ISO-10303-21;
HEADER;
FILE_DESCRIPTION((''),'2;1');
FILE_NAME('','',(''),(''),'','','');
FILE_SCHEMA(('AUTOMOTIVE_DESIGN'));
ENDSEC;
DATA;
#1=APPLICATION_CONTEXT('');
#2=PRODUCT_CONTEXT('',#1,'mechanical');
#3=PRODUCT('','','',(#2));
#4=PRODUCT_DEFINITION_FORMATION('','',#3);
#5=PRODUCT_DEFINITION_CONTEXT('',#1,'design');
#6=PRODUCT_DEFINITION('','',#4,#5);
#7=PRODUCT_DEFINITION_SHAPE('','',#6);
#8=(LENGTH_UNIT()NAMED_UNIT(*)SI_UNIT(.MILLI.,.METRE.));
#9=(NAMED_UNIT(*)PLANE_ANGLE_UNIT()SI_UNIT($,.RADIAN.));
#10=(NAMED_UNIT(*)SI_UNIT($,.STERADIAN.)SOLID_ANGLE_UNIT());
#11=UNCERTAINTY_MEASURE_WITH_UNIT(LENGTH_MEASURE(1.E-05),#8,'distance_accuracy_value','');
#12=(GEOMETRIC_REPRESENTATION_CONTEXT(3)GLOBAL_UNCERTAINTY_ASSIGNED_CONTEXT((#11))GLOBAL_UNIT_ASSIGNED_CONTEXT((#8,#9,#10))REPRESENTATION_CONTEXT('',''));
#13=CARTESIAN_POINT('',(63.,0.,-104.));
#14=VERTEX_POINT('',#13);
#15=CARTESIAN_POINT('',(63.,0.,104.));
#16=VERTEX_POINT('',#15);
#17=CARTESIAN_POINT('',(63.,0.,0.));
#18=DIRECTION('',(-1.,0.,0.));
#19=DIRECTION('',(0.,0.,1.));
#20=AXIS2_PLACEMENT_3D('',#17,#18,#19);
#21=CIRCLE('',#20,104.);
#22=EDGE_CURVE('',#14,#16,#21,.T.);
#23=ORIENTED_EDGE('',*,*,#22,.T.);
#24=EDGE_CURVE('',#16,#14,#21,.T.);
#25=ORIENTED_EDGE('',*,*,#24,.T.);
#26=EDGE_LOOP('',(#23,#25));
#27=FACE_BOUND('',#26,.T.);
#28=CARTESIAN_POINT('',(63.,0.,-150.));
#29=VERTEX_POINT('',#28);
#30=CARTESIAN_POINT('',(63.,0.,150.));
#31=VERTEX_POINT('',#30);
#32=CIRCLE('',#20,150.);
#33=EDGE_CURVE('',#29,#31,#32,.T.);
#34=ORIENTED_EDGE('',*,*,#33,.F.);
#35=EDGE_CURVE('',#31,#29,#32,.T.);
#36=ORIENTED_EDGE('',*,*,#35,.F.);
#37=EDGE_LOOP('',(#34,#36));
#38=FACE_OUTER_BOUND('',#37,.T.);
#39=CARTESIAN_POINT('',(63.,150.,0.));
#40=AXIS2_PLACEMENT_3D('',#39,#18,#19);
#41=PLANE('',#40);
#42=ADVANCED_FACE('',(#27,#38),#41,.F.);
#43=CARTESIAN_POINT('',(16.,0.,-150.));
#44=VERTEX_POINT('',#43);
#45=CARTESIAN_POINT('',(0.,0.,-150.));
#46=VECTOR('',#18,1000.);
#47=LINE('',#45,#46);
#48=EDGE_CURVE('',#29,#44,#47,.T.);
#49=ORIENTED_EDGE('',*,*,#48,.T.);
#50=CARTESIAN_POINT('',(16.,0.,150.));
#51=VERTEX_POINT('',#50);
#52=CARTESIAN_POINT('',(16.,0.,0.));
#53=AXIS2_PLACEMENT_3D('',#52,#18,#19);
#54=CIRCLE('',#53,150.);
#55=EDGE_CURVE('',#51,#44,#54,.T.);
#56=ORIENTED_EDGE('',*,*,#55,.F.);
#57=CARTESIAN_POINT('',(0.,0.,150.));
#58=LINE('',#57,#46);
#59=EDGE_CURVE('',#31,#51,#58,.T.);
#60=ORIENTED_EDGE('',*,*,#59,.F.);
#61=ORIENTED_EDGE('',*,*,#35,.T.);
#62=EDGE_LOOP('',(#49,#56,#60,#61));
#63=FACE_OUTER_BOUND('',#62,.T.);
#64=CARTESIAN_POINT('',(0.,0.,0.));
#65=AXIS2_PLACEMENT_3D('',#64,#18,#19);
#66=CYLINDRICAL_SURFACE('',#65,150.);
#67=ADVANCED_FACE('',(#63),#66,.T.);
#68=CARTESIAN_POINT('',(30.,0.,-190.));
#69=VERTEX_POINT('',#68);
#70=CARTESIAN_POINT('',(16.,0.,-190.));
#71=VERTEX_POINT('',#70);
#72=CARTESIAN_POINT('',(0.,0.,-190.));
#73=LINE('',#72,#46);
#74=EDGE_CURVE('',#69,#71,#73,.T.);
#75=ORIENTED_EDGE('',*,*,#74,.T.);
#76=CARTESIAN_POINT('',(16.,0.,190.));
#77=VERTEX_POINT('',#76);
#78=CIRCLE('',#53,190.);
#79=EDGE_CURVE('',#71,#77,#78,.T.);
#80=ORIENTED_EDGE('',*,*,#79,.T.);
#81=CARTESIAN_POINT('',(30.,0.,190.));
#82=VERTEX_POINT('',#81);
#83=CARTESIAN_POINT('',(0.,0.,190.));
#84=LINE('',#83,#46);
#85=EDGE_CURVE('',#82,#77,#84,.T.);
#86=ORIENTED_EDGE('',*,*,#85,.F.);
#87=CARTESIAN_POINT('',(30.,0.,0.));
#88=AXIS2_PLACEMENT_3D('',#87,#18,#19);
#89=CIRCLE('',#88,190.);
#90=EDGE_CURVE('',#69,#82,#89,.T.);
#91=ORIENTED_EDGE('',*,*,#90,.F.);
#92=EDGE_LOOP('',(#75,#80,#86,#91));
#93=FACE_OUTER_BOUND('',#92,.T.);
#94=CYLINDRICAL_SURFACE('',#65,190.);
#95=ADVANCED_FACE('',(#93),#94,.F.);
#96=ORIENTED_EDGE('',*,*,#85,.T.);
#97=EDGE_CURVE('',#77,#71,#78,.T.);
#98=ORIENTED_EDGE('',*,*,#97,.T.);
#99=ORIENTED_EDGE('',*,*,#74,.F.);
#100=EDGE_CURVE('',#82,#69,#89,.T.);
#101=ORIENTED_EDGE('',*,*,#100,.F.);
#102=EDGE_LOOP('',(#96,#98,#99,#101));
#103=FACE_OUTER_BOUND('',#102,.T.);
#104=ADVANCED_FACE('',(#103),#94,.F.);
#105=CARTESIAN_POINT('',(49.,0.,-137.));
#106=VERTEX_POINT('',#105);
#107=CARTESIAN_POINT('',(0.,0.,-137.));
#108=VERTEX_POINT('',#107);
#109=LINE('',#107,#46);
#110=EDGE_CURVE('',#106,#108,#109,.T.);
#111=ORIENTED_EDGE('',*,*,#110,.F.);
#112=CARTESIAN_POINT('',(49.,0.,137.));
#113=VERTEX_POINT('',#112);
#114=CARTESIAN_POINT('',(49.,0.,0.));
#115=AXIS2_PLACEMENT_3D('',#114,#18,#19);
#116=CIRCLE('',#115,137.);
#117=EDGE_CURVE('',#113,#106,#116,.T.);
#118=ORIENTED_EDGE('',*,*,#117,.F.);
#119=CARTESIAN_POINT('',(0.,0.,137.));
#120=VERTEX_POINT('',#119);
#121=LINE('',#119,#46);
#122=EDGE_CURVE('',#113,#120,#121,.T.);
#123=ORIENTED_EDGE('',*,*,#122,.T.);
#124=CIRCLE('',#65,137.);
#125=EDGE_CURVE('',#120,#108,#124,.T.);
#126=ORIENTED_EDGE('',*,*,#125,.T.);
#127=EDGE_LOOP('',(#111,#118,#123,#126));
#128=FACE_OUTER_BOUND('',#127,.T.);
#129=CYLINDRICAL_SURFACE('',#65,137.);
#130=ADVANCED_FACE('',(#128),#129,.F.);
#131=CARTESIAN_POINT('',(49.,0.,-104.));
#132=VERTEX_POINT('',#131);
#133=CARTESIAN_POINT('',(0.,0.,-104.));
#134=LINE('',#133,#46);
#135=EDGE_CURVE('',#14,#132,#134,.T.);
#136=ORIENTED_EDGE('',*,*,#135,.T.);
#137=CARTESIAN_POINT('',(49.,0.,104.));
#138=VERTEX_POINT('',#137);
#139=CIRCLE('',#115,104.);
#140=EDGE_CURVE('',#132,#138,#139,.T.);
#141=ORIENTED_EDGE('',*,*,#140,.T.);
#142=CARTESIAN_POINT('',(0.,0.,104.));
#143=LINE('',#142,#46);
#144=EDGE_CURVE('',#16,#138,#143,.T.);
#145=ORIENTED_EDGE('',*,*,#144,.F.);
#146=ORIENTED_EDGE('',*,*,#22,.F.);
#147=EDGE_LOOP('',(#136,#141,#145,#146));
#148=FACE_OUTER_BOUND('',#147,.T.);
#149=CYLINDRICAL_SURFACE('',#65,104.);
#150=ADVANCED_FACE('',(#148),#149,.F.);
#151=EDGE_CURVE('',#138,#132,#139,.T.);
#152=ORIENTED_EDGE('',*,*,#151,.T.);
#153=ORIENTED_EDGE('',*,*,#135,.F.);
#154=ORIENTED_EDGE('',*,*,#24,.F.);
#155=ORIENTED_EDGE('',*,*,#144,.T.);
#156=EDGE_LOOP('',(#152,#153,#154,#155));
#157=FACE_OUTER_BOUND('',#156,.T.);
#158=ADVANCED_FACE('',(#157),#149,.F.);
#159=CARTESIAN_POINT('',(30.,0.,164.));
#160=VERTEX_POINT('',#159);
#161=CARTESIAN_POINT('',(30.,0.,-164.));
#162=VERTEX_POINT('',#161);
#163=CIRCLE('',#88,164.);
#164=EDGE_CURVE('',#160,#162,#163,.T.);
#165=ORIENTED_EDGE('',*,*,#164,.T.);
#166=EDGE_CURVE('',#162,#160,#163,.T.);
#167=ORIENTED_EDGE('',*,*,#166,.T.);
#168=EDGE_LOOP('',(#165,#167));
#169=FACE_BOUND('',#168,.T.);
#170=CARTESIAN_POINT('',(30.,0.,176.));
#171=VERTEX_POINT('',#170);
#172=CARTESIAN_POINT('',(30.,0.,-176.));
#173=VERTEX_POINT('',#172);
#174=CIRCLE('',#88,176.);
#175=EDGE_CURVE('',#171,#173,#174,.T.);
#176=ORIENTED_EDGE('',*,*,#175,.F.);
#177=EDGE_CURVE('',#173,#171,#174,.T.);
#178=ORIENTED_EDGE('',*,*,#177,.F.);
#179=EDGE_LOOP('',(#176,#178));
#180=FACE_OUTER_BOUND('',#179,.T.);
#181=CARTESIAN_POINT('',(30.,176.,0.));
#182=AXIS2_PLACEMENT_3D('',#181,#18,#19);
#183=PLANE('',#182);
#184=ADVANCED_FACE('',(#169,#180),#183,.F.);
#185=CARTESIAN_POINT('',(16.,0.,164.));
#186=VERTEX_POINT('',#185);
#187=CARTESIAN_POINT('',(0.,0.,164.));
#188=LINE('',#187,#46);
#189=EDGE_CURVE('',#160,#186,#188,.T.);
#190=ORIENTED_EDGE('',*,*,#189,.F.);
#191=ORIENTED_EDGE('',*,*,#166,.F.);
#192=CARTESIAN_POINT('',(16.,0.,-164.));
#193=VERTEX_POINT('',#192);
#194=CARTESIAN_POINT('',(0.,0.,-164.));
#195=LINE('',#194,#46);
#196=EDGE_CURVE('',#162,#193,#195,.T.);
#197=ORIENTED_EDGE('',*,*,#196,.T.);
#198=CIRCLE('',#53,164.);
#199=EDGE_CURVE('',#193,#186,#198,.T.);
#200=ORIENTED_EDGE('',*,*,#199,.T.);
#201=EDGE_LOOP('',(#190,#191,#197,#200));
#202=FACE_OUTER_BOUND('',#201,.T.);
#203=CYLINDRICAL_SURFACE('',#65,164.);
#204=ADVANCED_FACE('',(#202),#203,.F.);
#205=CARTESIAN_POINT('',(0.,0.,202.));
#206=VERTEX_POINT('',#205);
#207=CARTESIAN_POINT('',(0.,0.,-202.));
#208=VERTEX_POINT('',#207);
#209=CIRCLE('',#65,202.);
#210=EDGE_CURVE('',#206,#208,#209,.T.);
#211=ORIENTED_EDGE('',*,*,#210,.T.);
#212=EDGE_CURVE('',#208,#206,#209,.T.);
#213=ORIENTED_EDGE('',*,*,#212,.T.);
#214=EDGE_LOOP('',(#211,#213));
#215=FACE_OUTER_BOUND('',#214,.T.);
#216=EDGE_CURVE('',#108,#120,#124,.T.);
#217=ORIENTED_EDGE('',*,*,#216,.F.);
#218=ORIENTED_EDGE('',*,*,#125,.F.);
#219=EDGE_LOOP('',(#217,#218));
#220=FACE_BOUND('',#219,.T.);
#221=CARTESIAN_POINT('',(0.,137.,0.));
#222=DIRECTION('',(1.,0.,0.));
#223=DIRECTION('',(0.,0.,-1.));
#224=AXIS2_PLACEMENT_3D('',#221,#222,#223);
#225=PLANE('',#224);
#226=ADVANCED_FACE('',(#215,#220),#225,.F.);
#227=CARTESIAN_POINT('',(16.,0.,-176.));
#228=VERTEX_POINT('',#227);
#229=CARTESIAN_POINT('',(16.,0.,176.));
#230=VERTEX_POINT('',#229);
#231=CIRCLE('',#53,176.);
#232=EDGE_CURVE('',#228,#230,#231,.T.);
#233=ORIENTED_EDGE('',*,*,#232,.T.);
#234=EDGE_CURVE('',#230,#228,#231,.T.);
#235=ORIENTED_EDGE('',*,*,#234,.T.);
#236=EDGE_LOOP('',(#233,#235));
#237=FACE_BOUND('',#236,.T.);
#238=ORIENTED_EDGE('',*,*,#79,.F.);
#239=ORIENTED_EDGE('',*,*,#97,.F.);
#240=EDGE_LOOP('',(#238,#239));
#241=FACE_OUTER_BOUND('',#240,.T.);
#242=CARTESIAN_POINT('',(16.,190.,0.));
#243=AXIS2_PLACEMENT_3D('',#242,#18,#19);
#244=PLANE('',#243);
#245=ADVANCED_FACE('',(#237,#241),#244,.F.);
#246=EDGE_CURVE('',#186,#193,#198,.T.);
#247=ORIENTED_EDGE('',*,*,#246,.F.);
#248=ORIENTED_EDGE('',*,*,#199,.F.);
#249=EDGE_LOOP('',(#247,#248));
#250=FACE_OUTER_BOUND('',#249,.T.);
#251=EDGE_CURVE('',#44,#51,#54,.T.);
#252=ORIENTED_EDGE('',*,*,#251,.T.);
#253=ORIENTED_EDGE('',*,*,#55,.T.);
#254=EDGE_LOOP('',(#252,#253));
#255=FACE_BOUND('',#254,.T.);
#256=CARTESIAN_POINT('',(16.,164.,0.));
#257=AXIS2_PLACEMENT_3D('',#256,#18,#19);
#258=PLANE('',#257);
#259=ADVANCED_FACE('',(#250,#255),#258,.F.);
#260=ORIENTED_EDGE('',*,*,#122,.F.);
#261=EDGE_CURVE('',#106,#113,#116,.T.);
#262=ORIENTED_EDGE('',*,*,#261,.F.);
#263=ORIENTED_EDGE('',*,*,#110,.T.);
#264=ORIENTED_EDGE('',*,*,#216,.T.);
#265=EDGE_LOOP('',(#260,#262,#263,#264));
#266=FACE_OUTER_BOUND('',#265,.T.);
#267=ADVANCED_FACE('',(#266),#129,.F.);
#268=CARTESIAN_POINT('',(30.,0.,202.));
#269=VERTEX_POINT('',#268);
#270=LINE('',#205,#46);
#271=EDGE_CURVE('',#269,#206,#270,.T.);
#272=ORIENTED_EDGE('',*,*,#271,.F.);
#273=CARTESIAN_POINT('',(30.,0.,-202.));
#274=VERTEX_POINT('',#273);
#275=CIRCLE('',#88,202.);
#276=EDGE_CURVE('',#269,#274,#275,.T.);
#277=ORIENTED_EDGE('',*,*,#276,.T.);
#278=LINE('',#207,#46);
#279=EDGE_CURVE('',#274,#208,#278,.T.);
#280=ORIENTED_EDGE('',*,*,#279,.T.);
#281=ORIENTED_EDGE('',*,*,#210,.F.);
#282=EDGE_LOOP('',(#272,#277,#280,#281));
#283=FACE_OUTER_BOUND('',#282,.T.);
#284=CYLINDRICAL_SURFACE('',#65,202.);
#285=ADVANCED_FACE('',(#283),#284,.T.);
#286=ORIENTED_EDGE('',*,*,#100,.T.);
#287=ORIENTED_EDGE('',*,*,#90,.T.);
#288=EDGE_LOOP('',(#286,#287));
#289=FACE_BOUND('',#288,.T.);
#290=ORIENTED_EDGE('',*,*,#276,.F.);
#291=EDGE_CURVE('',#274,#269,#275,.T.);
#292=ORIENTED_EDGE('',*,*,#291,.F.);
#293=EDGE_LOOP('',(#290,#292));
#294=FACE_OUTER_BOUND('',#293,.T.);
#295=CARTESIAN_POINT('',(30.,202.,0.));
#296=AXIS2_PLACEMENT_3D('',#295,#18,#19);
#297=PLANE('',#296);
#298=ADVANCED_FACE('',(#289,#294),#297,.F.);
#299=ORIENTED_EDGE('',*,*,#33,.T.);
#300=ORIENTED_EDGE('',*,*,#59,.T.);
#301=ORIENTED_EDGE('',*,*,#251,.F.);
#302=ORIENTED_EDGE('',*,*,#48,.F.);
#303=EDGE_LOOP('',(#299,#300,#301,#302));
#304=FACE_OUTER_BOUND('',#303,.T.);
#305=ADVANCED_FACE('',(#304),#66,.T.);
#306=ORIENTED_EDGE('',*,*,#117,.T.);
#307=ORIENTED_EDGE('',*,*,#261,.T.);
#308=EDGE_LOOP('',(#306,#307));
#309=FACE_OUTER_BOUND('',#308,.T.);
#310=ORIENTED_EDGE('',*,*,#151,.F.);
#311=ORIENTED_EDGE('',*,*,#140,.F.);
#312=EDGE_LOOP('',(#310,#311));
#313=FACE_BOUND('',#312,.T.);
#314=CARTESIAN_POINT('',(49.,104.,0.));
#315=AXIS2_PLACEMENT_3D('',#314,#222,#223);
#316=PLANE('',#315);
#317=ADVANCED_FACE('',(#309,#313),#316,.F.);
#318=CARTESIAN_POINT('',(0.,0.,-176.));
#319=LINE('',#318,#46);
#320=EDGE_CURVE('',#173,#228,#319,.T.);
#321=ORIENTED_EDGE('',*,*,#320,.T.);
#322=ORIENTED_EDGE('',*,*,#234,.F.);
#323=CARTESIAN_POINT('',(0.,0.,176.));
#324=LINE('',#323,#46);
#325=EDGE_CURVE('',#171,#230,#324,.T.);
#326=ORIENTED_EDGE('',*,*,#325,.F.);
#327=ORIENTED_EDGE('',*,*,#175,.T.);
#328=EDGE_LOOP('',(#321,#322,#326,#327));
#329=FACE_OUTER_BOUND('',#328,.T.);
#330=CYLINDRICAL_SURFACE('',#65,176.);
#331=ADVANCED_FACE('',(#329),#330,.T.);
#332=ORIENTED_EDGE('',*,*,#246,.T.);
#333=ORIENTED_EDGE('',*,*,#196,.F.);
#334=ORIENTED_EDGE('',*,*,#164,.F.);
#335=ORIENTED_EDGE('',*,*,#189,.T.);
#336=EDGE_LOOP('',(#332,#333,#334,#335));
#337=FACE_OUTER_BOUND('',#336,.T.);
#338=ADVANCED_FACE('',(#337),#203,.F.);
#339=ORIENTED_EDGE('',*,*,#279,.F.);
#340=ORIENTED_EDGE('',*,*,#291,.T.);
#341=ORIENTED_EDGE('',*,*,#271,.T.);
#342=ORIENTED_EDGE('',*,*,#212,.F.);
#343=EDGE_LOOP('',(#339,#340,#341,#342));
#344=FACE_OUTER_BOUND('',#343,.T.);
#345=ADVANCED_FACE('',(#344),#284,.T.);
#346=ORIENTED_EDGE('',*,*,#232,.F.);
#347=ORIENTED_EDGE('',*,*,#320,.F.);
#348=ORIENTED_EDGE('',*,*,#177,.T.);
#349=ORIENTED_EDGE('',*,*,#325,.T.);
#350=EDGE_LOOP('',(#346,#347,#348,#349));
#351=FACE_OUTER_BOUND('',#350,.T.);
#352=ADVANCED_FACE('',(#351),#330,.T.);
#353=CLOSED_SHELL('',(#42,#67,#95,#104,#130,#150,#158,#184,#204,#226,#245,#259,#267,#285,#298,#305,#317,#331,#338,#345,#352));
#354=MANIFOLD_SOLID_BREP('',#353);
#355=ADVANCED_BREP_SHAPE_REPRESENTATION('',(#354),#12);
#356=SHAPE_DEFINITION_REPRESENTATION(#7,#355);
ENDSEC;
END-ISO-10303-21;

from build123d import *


with BuildPart() as part:
    # Sketch2 → Revolve1 (revolve)
    with BuildSketch(Plane.XY, mode=Mode.PRIVATE) as revolve1_sk:
        Polygon((0, 137), (0, 202), (30, 202), (30, 190), (16, 190), (16, 176), (30, 176), (30, 164), (16, 164), (16, 150), (63, 150), (63, 104), (49, 104), (49, 137), align=None)
    revolve(revolve1_sk.sketch.rotate(Axis((0, 0, 0), (1, 0, 0)), 90), axis=Axis((0, 0, 0), (1, 0, 0)))


solid = part.part
